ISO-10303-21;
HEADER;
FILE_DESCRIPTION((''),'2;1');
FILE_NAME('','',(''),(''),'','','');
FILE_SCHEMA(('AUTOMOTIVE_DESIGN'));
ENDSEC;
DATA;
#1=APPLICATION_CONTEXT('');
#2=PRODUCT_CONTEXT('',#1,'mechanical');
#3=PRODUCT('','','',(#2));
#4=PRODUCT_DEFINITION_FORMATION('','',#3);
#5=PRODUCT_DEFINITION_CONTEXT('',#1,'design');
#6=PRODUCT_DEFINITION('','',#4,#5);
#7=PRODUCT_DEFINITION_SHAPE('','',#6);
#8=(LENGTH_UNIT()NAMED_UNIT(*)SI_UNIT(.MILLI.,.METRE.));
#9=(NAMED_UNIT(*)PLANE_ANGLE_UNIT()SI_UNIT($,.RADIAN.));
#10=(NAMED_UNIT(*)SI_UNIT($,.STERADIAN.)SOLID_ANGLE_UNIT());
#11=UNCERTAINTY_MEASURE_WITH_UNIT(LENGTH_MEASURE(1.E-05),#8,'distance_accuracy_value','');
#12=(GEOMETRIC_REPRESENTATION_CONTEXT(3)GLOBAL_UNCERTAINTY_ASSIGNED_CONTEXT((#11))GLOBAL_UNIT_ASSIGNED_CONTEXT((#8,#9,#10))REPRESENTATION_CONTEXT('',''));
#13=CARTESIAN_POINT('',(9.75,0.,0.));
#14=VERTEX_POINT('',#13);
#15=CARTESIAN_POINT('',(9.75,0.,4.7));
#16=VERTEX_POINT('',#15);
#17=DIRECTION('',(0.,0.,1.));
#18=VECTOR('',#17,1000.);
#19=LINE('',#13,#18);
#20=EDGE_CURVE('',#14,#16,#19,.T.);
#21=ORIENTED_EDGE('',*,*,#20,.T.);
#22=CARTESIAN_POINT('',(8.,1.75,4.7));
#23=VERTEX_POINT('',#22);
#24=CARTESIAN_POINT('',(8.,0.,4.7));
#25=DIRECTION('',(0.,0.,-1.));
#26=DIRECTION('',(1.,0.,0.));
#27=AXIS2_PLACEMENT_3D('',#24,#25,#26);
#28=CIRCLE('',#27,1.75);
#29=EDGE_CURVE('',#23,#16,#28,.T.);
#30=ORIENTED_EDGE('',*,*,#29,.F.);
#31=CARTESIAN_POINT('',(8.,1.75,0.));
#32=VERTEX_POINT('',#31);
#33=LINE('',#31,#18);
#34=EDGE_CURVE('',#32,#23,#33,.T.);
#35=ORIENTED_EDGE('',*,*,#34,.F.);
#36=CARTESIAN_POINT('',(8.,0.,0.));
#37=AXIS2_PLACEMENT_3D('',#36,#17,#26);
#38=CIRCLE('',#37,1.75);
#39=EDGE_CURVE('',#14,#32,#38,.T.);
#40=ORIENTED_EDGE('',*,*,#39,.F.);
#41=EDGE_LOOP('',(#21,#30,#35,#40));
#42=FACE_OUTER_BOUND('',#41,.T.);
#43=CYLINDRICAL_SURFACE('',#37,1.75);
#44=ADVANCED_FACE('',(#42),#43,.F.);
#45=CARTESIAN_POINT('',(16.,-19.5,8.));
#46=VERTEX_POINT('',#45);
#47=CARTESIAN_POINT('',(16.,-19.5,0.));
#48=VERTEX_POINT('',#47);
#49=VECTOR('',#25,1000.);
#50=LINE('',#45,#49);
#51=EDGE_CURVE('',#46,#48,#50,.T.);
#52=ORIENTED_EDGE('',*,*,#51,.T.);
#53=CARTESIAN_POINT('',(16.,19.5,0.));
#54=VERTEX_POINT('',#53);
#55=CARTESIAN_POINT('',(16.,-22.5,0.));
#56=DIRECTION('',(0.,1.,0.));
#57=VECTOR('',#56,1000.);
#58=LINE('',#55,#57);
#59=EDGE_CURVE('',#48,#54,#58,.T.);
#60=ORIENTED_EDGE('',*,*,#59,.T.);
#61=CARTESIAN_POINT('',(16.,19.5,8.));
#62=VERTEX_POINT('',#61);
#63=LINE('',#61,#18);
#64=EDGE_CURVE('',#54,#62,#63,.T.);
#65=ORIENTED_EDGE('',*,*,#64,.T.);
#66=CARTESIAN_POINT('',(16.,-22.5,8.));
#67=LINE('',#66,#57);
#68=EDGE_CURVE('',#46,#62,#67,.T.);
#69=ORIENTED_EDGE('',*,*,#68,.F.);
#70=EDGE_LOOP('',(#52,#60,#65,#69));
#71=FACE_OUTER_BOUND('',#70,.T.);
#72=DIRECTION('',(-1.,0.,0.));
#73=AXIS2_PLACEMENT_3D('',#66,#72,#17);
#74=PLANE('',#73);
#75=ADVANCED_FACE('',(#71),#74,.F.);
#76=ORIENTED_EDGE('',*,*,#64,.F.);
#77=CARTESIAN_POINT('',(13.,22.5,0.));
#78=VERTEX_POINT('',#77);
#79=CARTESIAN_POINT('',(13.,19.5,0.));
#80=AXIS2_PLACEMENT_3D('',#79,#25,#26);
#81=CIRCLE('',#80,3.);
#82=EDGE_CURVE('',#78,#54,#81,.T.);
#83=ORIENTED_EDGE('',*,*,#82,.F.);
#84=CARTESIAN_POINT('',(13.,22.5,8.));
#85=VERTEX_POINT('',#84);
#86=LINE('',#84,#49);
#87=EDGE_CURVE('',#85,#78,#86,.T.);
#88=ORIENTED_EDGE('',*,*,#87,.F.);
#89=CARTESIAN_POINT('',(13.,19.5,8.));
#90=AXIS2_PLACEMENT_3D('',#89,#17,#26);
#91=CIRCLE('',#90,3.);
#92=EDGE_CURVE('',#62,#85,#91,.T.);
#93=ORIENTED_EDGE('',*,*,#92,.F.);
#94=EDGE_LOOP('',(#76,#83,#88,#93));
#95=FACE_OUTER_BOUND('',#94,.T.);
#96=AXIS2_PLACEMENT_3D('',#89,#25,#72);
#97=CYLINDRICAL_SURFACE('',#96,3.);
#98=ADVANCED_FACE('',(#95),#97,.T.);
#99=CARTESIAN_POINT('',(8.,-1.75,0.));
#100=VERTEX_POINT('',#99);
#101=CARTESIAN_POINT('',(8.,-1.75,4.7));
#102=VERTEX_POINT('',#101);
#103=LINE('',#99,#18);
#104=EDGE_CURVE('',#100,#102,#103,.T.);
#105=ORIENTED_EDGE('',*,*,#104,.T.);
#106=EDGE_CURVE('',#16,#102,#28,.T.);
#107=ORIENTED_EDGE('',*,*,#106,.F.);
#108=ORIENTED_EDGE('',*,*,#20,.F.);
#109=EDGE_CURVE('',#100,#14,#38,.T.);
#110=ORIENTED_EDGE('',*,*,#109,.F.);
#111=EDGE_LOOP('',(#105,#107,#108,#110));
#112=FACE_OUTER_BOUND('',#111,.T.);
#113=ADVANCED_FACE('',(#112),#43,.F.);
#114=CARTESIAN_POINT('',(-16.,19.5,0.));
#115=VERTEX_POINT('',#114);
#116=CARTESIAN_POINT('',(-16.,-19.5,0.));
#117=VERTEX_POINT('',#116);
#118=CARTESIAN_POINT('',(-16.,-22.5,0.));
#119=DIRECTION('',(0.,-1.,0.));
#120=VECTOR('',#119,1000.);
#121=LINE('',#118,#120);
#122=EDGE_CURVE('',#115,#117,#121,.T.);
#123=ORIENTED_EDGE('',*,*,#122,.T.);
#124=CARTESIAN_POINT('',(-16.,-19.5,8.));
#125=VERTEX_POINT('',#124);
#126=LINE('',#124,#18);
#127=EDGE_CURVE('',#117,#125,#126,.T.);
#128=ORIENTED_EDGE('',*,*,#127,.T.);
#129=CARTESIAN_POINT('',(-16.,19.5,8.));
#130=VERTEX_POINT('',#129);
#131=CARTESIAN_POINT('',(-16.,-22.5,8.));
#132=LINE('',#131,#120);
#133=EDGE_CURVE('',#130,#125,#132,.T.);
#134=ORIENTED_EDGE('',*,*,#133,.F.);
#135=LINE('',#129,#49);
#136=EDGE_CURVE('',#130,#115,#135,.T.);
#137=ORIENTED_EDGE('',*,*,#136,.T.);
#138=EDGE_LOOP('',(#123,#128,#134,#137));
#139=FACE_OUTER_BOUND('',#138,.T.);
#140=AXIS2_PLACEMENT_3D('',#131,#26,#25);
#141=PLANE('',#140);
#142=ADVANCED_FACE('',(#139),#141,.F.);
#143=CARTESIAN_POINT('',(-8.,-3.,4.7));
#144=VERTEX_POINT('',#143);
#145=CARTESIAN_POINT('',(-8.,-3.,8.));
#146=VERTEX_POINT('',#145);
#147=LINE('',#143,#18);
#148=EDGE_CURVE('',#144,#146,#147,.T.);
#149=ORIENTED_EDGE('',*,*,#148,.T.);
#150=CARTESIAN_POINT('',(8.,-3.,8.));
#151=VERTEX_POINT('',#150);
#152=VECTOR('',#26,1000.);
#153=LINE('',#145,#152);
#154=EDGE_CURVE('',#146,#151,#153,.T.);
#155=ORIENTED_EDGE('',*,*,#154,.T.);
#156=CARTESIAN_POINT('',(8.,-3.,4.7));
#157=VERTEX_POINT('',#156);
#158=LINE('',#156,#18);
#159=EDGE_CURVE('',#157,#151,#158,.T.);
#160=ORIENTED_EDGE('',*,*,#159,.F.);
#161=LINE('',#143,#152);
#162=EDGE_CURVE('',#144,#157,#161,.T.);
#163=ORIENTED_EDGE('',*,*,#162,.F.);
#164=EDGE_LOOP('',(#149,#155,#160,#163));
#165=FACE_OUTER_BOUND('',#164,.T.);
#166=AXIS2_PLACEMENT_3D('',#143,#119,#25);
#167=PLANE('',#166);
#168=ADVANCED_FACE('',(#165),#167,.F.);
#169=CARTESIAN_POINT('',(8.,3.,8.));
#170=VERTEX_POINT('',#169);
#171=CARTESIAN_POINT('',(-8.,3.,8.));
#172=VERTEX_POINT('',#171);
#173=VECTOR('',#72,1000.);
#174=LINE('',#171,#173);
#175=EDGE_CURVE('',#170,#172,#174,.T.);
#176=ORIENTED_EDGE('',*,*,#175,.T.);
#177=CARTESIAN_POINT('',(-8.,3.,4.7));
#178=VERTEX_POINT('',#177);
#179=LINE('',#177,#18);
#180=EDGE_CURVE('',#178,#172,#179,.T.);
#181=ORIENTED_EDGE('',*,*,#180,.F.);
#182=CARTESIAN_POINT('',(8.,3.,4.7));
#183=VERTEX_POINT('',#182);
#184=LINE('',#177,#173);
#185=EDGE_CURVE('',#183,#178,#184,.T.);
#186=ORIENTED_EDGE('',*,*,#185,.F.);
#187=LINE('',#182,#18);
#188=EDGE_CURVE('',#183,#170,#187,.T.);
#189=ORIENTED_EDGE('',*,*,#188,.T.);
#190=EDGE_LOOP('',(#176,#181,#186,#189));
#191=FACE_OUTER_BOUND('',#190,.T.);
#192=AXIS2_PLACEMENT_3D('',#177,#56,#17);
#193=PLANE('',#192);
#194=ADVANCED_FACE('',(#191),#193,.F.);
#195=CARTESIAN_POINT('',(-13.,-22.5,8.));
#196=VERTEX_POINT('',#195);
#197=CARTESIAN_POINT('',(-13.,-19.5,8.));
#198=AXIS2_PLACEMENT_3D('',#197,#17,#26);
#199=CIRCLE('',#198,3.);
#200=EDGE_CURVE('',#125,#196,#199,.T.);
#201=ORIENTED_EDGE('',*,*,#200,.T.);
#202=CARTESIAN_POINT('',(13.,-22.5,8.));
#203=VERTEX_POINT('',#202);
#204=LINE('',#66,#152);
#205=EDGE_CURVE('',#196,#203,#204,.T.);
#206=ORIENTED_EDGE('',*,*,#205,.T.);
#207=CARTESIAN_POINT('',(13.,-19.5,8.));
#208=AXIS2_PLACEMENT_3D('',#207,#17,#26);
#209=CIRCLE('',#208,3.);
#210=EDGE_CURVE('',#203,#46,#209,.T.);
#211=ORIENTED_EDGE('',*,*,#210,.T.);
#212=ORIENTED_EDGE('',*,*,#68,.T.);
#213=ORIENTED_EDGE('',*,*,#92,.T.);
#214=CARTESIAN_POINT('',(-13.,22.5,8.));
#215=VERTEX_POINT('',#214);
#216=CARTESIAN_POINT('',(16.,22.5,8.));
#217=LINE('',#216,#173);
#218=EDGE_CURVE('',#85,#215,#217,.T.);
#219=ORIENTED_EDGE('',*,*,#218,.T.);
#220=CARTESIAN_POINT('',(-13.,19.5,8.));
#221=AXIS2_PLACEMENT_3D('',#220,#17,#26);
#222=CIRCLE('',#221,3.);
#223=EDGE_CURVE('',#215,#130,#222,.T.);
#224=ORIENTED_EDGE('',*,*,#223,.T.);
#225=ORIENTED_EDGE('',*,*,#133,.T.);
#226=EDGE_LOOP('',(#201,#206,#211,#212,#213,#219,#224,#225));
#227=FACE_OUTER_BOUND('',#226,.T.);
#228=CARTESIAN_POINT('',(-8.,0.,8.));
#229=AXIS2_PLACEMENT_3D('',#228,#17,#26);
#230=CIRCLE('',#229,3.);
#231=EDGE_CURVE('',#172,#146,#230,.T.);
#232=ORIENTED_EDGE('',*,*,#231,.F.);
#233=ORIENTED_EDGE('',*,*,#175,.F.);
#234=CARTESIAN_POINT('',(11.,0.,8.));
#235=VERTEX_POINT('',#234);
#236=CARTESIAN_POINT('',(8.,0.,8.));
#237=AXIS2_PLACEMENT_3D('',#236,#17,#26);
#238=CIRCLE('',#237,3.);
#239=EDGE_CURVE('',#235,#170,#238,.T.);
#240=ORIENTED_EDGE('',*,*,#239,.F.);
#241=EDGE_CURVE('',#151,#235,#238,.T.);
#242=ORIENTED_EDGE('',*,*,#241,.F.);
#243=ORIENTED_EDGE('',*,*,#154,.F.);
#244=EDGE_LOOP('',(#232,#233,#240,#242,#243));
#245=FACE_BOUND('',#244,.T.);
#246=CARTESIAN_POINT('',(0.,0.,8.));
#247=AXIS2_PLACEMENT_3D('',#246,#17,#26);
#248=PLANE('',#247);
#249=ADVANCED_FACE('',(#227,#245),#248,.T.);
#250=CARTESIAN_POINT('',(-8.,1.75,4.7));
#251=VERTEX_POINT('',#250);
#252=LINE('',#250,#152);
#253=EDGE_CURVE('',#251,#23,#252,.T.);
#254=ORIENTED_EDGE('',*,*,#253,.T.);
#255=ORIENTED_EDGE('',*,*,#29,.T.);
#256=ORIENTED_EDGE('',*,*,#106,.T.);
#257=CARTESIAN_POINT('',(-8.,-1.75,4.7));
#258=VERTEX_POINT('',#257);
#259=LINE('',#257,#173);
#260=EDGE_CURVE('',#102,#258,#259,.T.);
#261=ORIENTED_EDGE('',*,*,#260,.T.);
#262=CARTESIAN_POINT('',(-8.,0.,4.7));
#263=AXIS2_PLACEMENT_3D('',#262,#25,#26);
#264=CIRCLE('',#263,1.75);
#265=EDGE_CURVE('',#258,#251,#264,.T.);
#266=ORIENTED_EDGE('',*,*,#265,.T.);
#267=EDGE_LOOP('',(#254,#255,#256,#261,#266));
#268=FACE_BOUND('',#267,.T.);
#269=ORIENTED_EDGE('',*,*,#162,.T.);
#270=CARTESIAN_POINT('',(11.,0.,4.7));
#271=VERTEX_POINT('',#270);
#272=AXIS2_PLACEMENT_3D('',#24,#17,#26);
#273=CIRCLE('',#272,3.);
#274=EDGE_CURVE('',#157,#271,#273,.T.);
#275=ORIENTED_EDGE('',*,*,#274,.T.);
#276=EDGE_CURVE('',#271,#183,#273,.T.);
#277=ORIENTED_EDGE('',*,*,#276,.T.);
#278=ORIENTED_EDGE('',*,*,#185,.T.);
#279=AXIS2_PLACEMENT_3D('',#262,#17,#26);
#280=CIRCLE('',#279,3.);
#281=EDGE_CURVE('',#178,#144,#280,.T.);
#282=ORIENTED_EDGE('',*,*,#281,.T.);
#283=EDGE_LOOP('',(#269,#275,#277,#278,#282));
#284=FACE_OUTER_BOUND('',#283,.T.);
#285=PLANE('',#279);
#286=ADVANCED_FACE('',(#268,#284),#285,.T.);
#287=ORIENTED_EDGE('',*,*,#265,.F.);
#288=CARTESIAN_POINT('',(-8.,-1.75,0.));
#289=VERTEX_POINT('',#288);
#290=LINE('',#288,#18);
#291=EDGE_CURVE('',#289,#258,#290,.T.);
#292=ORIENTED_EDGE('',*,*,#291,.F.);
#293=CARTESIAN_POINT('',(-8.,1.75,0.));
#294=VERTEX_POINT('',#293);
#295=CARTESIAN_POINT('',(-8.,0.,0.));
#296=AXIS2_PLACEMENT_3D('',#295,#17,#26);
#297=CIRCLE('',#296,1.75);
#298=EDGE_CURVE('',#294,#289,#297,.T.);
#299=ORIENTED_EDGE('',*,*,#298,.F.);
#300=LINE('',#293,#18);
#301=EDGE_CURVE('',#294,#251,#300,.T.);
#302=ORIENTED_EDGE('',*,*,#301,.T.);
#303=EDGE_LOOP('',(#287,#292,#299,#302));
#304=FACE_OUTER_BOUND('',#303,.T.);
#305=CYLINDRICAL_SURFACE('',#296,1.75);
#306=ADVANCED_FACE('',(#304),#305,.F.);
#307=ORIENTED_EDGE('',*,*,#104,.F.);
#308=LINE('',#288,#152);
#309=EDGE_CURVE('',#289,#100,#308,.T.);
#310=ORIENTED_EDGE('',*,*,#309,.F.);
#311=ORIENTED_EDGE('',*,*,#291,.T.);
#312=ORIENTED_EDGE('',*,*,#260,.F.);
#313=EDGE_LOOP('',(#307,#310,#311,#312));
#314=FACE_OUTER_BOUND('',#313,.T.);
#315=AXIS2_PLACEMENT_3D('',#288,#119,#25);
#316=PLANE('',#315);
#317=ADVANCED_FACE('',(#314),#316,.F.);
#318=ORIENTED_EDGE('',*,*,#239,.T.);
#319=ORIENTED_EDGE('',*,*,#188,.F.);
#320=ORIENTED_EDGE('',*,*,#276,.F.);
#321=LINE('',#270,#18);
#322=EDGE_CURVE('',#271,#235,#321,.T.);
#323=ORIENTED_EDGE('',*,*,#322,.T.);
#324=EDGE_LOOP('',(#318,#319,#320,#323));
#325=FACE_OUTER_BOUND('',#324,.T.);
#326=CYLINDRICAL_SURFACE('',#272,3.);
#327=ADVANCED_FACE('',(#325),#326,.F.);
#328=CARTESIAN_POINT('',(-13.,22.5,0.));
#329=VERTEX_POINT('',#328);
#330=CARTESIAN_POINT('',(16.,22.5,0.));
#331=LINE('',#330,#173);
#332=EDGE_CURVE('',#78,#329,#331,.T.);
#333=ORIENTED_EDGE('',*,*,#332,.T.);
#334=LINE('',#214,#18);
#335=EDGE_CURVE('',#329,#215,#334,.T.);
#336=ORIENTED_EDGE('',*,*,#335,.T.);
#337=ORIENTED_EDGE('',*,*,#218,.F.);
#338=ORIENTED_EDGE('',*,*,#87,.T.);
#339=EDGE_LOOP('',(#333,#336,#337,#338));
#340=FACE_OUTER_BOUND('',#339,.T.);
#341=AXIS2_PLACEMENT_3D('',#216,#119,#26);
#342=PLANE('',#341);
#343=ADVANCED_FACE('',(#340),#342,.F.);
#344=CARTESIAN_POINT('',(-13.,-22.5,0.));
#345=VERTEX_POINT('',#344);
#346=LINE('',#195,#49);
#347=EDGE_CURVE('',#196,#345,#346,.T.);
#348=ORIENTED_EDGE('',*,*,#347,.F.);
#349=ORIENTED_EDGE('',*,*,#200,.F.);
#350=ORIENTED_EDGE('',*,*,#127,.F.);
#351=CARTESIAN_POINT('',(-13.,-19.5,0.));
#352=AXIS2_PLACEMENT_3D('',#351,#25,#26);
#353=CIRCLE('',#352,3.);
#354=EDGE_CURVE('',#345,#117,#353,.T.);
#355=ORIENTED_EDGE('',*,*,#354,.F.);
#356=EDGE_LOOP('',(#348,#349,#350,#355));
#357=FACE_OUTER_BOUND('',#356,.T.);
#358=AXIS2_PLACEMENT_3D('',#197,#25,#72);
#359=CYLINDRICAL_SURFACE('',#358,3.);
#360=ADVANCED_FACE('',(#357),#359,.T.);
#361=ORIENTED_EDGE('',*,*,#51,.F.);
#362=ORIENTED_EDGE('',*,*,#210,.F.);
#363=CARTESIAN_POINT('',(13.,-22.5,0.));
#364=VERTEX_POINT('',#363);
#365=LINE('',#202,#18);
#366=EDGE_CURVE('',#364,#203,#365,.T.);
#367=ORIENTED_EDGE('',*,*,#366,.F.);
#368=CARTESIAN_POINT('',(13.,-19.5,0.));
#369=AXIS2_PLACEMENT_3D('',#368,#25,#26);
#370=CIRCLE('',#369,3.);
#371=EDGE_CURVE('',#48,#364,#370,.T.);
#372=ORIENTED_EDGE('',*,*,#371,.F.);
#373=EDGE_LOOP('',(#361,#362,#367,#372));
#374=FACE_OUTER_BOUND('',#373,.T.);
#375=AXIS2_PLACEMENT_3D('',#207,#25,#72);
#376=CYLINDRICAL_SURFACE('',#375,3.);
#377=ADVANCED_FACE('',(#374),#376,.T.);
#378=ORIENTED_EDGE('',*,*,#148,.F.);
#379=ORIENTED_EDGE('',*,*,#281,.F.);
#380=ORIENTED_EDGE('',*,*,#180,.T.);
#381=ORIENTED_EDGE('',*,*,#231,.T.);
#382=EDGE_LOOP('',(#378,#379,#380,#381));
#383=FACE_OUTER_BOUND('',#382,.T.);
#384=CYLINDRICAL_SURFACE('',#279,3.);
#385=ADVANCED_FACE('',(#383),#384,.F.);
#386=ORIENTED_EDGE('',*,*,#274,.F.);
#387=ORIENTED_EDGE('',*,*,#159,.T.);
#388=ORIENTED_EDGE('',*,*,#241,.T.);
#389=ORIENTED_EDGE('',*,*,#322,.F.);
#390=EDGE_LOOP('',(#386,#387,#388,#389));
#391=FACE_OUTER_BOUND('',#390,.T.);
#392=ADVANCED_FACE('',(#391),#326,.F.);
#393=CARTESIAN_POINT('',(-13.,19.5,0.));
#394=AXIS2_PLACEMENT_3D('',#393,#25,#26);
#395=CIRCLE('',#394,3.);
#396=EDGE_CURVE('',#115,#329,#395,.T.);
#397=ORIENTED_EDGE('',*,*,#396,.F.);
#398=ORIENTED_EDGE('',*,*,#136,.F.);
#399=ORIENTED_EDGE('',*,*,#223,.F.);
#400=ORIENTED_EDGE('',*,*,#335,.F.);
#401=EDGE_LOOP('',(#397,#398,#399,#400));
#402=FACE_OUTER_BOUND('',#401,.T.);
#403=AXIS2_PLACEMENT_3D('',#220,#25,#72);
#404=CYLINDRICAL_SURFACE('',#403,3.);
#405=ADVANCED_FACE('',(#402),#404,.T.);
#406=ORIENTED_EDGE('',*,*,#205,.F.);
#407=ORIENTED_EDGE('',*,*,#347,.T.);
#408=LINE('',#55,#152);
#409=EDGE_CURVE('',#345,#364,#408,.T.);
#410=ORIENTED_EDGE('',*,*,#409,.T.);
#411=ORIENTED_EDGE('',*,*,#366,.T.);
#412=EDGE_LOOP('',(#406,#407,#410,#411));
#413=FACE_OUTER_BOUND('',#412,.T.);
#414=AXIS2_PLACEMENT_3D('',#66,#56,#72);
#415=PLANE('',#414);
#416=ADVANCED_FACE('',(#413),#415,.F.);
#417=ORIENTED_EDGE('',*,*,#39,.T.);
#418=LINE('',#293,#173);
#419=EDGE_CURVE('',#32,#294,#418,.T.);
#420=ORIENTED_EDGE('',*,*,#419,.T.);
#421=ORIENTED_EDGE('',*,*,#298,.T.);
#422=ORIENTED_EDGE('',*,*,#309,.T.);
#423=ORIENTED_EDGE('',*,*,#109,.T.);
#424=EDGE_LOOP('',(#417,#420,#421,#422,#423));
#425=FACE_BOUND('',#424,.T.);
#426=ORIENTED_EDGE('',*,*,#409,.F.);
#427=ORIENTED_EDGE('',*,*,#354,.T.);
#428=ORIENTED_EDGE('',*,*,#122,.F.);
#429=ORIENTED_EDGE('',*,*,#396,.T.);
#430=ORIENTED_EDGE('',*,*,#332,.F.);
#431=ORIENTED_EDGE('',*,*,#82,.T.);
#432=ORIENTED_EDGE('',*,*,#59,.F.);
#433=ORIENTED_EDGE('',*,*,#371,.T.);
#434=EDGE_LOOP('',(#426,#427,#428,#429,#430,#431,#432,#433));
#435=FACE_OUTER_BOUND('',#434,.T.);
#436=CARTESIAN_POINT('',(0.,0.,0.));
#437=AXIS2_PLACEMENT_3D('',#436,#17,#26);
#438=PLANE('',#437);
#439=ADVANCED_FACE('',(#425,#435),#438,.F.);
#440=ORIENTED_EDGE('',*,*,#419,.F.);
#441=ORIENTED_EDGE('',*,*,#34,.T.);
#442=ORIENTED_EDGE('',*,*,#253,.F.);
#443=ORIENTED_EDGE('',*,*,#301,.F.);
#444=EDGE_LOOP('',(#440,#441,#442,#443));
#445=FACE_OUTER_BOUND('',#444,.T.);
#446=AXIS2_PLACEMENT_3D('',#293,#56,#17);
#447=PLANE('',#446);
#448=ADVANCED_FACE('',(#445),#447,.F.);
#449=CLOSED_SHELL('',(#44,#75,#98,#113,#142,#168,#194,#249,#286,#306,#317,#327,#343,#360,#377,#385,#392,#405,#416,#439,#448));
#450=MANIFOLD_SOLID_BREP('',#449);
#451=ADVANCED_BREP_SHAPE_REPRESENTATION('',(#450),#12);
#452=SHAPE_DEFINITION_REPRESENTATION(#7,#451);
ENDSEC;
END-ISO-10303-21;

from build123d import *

# Parameters (mm, degrees)
SKETCH1_W           = 32
SKETCH1_H           = 45
BOSS_EXTRUDE1_DEPTH = 8
CUT_EXTRUDE1_DEPTH  = 29.744564704
CUT_EXTRUDE2_DEPTH  = 3.3
FILLET1_R           = 3


with BuildPart() as part:
    # Sketch1 → Boss-Extrude1 (new body)
    with BuildSketch(Plane.XY):
        Rectangle(SKETCH1_W, SKETCH1_H)
    extrude(amount=BOSS_EXTRUDE1_DEPTH)

    # Sketch5 → Cut-Extrude1 (cut, through all)
    with BuildSketch(Plane.XY.offset(8)):
        with BuildLine():
            Line((-8, 1.75), (8, 1.75))
            ThreePointArc((8, 1.75), (9.75, 0), (8, -1.75))
            Line((8, -1.75), (-8, -1.75))
            ThreePointArc((-8, -1.75), (-9.75, 0), (-8, 1.75))
        make_face()
    extrude(amount=-CUT_EXTRUDE1_DEPTH, mode=Mode.SUBTRACT)

    # Sketch6 → Cut-Extrude2 (cut)
    with BuildSketch(Plane.XY.offset(8)):
        with BuildLine():
            Line((-8, 3), (8, 3))
            ThreePointArc((8, 3), (11, 0), (8, -3))
            Line((8, -3), (-8, -3))
            ThreePointArc((-8, -3), (-11, 0), (-8, 3))
        make_face()
    extrude(amount=-CUT_EXTRUDE2_DEPTH, mode=Mode.SUBTRACT)

    # Fillet1
    fillet1_edges = [part.edges().sort_by_distance(p)[0] for p in [
        (-16, 22.5, 4),
        (16, 22.5, 4),
        (16, -22.5, 4),
        (-16, -22.5, 4),
    ]]
    fillet(fillet1_edges, radius=FILLET1_R)


solid = part.part
